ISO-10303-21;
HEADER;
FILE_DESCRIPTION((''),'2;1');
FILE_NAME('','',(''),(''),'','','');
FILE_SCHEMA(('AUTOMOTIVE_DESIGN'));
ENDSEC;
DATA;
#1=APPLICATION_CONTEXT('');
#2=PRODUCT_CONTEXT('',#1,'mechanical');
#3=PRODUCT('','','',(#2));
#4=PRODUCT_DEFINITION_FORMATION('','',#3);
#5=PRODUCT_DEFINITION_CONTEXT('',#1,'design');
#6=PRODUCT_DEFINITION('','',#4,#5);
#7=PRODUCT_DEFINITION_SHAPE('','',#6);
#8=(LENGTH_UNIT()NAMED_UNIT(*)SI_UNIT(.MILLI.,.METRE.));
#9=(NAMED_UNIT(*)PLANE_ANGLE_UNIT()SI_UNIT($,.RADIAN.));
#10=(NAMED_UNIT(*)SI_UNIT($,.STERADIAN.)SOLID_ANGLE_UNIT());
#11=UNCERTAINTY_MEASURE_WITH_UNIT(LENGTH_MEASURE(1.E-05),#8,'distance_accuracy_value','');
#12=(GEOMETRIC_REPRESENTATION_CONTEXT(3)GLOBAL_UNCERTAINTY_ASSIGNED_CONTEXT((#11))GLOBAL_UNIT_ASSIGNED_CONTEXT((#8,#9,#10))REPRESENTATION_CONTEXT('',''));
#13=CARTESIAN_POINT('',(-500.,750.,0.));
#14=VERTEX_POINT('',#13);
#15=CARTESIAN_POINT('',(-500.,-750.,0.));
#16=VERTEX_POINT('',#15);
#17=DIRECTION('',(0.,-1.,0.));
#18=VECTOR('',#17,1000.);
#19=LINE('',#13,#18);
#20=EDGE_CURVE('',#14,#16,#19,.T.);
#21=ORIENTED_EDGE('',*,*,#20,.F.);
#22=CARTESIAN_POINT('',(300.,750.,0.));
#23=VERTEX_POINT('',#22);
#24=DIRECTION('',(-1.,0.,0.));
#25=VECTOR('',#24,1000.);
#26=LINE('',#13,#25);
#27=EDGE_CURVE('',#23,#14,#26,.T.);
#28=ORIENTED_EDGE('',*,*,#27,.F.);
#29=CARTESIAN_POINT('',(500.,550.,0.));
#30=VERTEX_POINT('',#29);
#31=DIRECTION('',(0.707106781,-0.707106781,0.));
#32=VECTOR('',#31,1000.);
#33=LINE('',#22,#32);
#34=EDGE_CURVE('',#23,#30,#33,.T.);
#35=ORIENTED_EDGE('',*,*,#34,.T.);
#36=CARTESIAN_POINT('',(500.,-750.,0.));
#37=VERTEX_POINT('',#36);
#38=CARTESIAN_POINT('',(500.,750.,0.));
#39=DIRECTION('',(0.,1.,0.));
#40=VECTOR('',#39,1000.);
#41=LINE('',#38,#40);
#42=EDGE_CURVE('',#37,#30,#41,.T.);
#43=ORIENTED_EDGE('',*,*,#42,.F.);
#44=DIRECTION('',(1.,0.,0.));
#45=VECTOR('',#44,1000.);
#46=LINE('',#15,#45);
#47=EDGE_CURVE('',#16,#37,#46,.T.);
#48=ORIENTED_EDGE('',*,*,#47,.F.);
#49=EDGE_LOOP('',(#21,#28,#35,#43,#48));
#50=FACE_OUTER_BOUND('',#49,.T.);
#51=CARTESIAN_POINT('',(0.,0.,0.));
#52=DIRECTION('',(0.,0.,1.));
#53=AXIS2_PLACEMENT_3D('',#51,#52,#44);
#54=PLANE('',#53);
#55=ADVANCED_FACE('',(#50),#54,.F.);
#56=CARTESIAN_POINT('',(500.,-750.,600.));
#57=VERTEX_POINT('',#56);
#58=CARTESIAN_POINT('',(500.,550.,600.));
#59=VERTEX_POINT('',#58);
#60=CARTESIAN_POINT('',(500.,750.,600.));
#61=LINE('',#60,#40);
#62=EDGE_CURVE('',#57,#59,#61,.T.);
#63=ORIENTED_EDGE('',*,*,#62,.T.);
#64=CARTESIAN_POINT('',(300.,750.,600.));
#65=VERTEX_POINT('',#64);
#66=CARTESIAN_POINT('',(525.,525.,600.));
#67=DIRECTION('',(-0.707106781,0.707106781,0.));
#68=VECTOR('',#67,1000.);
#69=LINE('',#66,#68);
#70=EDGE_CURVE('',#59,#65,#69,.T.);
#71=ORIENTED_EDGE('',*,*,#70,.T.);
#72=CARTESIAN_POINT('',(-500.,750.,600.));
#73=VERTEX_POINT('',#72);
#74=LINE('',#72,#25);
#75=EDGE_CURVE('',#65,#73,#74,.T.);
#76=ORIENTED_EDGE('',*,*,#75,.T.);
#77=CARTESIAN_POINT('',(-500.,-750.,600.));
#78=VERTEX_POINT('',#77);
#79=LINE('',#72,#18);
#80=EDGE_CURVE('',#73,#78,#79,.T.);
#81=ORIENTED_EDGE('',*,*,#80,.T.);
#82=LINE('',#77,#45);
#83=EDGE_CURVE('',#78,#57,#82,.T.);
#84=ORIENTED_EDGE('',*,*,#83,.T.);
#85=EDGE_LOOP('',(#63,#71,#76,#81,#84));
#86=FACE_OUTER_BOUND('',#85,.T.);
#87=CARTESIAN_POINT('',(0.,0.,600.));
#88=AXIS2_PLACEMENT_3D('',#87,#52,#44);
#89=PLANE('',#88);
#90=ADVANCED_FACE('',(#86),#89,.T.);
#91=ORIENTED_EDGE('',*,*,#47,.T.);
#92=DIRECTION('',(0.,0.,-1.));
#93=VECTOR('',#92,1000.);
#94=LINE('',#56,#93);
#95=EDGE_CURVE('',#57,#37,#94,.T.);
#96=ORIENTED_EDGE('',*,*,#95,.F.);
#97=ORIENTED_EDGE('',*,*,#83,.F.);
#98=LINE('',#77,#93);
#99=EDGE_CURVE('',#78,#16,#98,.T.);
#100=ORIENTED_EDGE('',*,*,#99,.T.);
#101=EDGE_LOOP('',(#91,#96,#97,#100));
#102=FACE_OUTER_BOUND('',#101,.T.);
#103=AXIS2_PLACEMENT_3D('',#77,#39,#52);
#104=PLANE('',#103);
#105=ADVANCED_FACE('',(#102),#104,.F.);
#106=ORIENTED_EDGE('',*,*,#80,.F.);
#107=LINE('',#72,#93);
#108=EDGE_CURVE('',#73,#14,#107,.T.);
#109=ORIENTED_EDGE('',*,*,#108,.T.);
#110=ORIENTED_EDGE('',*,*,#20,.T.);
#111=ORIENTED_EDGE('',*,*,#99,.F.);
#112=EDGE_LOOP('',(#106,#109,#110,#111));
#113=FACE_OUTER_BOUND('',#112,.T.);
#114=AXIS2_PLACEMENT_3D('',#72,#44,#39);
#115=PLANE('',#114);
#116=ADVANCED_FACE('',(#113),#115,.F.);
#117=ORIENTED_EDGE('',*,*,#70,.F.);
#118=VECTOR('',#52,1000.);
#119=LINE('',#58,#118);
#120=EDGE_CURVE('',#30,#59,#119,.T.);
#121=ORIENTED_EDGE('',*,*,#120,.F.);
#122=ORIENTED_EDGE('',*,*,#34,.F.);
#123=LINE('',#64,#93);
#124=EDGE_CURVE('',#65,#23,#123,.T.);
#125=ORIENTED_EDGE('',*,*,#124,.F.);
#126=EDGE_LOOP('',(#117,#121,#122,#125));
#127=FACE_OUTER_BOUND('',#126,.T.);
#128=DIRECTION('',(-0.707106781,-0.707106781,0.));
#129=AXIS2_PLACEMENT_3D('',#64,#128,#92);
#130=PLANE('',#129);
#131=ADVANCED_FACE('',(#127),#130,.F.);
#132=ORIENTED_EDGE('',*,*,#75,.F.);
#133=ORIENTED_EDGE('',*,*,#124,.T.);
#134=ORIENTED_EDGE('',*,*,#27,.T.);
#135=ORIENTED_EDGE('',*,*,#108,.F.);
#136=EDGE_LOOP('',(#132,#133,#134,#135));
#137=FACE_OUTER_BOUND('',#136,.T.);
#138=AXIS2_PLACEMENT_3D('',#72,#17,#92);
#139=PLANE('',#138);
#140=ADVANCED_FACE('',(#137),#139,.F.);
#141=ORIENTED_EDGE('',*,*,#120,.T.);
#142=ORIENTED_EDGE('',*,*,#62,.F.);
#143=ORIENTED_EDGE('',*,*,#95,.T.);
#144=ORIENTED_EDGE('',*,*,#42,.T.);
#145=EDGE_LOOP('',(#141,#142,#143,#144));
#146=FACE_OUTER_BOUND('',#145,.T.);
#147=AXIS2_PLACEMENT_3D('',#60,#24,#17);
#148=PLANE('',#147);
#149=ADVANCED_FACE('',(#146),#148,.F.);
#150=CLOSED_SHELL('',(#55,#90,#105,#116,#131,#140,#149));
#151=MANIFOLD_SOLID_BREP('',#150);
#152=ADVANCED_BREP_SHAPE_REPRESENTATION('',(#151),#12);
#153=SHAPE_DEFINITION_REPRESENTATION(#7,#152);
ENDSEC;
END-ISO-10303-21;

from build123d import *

# Parameters (mm, degrees)
SKETCH1_W           = 1000
SKETCH1_H           = 1500
BOSS_EXTRUDE1_DEPTH = 600
CHAMFER1_SIZE       = 200


with BuildPart() as part:
    # Sketch1 → Boss-Extrude1 (new body)
    with BuildSketch(Plane.XY):
        Rectangle(SKETCH1_W, SKETCH1_H)
    extrude(amount=BOSS_EXTRUDE1_DEPTH)

    # Chamfer1
    chamfer1_edges = [part.edges().sort_by_distance(p)[0] for p in [
        (500, 750, 300),
    ]]
    chamfer(chamfer1_edges, length=CHAMFER1_SIZE)


solid = part.part
